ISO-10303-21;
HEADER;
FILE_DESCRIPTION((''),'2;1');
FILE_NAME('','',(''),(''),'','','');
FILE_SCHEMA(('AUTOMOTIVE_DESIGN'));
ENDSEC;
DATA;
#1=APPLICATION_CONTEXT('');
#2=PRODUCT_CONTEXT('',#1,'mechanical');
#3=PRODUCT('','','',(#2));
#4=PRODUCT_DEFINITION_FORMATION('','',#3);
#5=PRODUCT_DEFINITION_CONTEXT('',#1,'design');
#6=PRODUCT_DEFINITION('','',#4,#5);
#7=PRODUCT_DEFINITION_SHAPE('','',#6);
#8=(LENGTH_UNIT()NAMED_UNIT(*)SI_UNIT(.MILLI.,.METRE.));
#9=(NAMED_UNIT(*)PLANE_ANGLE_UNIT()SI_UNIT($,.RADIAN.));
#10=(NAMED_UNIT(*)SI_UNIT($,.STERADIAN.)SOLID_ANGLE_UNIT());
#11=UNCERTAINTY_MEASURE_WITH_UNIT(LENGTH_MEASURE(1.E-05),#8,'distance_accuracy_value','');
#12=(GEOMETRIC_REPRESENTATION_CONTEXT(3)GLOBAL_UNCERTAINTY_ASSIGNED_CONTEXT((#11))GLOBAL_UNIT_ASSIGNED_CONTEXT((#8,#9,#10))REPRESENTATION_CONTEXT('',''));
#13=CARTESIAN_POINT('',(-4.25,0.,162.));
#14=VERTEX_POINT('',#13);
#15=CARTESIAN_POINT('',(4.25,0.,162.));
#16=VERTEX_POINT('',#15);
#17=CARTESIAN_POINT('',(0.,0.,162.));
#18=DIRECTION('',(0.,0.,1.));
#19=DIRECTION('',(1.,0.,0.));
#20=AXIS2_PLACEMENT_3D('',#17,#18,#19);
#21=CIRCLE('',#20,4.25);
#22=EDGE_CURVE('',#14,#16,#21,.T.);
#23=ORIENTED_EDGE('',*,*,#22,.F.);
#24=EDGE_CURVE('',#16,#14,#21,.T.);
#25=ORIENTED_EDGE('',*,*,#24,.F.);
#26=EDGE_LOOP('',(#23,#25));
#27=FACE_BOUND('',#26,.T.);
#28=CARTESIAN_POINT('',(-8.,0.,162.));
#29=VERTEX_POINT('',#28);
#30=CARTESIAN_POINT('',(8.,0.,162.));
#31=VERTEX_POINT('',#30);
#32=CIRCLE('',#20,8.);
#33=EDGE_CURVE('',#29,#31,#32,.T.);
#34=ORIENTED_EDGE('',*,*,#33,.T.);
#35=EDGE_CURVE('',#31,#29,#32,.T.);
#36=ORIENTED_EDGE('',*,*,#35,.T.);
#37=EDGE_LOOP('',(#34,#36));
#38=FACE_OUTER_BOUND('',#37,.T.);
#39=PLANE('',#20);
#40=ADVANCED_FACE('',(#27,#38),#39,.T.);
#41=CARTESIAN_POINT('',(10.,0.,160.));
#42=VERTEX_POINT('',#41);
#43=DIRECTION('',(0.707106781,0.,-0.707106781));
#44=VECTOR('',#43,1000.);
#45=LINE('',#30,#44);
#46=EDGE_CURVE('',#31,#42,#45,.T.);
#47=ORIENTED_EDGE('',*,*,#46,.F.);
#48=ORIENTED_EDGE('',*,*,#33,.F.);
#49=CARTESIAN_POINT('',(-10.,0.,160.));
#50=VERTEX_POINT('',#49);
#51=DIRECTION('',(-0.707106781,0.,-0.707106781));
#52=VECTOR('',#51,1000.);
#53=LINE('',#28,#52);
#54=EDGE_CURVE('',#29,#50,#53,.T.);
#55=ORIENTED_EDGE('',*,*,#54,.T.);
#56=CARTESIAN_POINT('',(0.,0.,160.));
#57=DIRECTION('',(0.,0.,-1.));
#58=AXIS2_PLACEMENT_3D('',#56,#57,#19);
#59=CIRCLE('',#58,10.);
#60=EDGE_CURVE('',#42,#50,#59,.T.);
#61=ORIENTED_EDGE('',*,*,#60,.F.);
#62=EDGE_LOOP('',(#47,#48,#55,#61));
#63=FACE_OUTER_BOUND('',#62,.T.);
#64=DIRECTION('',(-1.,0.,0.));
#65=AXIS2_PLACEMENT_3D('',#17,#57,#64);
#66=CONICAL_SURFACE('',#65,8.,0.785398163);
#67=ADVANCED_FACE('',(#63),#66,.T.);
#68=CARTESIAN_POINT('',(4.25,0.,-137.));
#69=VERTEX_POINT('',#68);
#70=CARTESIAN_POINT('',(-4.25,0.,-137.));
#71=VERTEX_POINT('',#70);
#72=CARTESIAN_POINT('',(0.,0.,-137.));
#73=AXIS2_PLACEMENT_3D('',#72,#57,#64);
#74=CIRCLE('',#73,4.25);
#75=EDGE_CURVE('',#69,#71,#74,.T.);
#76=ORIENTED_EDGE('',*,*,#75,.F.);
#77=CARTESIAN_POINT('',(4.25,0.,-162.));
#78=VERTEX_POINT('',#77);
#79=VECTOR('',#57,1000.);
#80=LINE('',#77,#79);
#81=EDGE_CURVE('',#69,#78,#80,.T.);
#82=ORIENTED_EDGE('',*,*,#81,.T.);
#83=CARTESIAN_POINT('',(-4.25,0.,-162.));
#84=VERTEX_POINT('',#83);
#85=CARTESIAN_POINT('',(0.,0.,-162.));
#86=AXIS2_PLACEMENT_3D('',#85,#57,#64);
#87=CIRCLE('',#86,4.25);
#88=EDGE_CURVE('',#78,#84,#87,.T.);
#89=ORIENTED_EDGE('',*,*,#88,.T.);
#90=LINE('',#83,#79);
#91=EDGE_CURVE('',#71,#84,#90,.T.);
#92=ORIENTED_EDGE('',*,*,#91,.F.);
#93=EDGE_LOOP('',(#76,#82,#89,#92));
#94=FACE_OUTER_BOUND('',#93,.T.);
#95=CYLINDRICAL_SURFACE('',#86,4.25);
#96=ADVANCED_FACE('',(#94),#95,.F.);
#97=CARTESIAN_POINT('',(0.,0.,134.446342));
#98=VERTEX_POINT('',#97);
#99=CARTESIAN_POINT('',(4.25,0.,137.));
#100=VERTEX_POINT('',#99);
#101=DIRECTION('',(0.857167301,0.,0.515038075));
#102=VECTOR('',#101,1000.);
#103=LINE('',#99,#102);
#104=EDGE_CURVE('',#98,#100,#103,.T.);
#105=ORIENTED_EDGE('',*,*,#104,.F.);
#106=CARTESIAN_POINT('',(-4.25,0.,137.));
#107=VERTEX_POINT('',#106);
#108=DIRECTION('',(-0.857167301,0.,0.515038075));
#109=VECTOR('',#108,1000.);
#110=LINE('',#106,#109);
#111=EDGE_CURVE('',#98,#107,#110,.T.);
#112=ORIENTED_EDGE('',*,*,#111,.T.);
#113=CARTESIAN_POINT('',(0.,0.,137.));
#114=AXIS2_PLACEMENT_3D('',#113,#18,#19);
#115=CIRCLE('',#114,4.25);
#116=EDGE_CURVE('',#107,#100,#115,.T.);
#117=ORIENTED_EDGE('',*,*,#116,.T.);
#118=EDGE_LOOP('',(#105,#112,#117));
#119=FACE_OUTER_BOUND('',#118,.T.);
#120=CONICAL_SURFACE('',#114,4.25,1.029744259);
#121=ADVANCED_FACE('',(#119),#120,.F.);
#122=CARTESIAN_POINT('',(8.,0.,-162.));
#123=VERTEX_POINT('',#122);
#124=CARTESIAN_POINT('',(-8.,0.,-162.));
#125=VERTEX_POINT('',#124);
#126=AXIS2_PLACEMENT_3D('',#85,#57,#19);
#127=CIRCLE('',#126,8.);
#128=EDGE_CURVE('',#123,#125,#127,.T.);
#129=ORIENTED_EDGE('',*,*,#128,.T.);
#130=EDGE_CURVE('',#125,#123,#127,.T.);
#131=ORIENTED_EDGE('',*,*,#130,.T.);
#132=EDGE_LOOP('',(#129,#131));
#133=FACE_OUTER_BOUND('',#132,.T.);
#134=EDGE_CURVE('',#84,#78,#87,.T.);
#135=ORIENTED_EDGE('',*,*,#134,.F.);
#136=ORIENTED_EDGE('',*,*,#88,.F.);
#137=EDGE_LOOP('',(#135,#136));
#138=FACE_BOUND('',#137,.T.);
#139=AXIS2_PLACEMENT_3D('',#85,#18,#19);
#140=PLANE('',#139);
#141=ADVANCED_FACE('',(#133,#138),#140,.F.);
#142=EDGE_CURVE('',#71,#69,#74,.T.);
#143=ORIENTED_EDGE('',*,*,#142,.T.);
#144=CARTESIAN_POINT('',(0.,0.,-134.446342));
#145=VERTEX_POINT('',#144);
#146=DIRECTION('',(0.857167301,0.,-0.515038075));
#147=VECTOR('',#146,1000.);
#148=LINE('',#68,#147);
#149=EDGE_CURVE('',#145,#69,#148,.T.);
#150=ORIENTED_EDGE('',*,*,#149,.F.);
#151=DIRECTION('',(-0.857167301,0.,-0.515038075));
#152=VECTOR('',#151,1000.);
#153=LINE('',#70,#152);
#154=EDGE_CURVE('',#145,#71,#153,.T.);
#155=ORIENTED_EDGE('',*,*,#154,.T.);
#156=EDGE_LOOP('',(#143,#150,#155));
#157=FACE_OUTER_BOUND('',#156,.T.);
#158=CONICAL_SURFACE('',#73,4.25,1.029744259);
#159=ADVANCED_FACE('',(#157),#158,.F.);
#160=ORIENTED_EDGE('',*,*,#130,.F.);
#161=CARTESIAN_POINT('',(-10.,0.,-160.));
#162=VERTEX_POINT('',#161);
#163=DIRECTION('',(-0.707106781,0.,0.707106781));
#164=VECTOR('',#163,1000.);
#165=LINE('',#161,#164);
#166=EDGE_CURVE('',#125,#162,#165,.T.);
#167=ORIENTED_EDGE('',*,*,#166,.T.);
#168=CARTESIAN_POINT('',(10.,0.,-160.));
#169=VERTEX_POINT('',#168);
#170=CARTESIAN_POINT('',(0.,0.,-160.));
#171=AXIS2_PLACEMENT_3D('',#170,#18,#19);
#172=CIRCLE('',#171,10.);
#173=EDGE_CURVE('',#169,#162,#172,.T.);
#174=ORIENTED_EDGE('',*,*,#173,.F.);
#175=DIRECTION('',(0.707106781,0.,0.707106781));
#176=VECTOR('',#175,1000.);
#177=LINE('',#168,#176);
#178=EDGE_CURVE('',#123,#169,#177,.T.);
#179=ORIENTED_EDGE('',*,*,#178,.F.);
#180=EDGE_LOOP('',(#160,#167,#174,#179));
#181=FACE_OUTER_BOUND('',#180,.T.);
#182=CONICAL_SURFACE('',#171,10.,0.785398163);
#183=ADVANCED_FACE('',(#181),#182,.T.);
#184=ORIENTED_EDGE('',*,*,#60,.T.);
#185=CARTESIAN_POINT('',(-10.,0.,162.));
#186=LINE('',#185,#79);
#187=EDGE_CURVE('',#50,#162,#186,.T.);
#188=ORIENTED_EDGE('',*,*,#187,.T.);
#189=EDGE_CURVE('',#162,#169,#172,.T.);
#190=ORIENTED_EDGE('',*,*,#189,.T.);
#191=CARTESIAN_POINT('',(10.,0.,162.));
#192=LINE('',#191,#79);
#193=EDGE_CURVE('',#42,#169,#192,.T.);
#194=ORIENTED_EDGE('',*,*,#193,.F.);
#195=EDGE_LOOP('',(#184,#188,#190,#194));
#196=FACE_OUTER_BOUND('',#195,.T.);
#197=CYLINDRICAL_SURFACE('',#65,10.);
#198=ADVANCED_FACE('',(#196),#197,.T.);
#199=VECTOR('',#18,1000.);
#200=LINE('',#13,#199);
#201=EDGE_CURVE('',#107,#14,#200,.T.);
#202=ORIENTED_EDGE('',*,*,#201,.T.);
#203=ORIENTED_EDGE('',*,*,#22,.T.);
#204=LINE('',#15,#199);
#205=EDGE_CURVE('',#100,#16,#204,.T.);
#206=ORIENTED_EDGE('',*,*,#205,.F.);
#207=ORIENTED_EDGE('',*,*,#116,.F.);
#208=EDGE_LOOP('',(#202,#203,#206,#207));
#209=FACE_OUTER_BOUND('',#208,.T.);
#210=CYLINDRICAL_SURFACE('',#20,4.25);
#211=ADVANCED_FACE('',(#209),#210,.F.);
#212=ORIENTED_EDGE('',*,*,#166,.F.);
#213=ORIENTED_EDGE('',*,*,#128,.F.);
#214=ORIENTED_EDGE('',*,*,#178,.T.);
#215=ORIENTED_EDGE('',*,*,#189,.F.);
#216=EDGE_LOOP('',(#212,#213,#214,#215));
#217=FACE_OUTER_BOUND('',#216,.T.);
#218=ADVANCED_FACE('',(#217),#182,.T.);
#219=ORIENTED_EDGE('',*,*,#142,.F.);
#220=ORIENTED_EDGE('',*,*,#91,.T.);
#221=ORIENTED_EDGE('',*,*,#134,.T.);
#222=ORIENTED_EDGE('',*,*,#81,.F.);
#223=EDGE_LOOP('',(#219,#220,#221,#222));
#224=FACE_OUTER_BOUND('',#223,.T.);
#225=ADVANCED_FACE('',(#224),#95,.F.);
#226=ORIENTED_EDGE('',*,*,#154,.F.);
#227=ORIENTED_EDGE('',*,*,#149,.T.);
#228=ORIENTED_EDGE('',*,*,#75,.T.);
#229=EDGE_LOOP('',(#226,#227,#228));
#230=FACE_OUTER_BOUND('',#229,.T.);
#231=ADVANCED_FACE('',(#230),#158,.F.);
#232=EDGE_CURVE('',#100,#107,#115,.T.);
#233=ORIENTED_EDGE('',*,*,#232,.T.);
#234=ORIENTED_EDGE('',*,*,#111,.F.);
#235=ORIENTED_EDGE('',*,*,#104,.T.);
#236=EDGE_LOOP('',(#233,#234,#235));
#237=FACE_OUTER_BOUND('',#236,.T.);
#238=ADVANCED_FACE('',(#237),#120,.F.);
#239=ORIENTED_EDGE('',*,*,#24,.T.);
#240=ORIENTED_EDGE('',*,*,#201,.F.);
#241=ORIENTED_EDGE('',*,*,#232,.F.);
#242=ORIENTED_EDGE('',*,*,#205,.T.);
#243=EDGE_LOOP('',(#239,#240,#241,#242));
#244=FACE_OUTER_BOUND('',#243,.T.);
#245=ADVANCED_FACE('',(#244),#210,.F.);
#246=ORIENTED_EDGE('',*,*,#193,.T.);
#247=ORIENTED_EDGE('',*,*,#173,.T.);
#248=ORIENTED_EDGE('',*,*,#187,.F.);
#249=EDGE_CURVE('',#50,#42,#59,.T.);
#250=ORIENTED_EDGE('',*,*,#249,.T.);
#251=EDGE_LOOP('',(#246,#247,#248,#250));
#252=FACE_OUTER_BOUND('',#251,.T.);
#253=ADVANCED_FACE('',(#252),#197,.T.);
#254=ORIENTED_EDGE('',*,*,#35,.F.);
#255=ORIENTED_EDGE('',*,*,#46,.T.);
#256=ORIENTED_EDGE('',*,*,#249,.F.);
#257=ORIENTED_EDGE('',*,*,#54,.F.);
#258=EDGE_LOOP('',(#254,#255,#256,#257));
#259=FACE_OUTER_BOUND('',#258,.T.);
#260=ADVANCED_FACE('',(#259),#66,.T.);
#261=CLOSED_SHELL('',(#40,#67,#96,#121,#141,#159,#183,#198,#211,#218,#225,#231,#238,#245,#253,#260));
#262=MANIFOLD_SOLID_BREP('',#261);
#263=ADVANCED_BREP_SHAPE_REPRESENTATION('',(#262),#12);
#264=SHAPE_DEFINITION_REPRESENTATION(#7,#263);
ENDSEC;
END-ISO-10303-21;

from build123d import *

# Parameters (mm, degrees)
SKETCH_1_R              = 10
EXTRUDE_1_DEPTH         = 162
CHAMFER_1_SIZE          = 2
HOLE_WIZARD_M10_1_D     = 8.5
HOLE_WIZARD_M10_1_DEPTH = 25
HOLE_WIZARD_M10_1_TIP   = 2.553657631
HOLE_WIZARD_M10_2_D     = 8.5
HOLE_WIZARD_M10_2_DEPTH = 25
HOLE_WIZARD_M10_2_TIP   = 2.553657631


with BuildPart() as part:
    # 草图1 → 凸台-拉伸1 (new, symmetric)
    with BuildSketch(Plane.XY):
        Circle(SKETCH_1_R)
    extrude(amount=EXTRUDE_1_DEPTH, both=True)

    # 倒角1
    chamfer_1_edges = [part.edges().sort_by_distance(p)[0] for p in [
        (-10, 0, -162),
        (-10, 0, 162),
    ]]
    chamfer(chamfer_1_edges, length=CHAMFER_1_SIZE)

    # M10 螺纹孔1
    with Locations(Plane.XY.offset(162)):
        with Locations((0, 0)):
            Hole(HOLE_WIZARD_M10_1_D / 2, depth=HOLE_WIZARD_M10_1_DEPTH)
            with Locations((0, 0, -(HOLE_WIZARD_M10_1_DEPTH + HOLE_WIZARD_M10_1_TIP / 2))):  # 118° drill point
                Cone(0, HOLE_WIZARD_M10_1_D / 2, HOLE_WIZARD_M10_1_TIP, mode=Mode.SUBTRACT)

    # M10 螺纹孔2
    with Locations(Plane(origin=(0, 0, -162), x_dir=(-1, 0, 0), z_dir=(0, 0, -1))):
        with Locations((0, 0)):
            Hole(HOLE_WIZARD_M10_2_D / 2, depth=HOLE_WIZARD_M10_2_DEPTH)
            with Locations((0, 0, -(HOLE_WIZARD_M10_2_DEPTH + HOLE_WIZARD_M10_2_TIP / 2))):  # 118° drill point
                Cone(0, HOLE_WIZARD_M10_2_D / 2, HOLE_WIZARD_M10_2_TIP, mode=Mode.SUBTRACT)


solid = part.part
